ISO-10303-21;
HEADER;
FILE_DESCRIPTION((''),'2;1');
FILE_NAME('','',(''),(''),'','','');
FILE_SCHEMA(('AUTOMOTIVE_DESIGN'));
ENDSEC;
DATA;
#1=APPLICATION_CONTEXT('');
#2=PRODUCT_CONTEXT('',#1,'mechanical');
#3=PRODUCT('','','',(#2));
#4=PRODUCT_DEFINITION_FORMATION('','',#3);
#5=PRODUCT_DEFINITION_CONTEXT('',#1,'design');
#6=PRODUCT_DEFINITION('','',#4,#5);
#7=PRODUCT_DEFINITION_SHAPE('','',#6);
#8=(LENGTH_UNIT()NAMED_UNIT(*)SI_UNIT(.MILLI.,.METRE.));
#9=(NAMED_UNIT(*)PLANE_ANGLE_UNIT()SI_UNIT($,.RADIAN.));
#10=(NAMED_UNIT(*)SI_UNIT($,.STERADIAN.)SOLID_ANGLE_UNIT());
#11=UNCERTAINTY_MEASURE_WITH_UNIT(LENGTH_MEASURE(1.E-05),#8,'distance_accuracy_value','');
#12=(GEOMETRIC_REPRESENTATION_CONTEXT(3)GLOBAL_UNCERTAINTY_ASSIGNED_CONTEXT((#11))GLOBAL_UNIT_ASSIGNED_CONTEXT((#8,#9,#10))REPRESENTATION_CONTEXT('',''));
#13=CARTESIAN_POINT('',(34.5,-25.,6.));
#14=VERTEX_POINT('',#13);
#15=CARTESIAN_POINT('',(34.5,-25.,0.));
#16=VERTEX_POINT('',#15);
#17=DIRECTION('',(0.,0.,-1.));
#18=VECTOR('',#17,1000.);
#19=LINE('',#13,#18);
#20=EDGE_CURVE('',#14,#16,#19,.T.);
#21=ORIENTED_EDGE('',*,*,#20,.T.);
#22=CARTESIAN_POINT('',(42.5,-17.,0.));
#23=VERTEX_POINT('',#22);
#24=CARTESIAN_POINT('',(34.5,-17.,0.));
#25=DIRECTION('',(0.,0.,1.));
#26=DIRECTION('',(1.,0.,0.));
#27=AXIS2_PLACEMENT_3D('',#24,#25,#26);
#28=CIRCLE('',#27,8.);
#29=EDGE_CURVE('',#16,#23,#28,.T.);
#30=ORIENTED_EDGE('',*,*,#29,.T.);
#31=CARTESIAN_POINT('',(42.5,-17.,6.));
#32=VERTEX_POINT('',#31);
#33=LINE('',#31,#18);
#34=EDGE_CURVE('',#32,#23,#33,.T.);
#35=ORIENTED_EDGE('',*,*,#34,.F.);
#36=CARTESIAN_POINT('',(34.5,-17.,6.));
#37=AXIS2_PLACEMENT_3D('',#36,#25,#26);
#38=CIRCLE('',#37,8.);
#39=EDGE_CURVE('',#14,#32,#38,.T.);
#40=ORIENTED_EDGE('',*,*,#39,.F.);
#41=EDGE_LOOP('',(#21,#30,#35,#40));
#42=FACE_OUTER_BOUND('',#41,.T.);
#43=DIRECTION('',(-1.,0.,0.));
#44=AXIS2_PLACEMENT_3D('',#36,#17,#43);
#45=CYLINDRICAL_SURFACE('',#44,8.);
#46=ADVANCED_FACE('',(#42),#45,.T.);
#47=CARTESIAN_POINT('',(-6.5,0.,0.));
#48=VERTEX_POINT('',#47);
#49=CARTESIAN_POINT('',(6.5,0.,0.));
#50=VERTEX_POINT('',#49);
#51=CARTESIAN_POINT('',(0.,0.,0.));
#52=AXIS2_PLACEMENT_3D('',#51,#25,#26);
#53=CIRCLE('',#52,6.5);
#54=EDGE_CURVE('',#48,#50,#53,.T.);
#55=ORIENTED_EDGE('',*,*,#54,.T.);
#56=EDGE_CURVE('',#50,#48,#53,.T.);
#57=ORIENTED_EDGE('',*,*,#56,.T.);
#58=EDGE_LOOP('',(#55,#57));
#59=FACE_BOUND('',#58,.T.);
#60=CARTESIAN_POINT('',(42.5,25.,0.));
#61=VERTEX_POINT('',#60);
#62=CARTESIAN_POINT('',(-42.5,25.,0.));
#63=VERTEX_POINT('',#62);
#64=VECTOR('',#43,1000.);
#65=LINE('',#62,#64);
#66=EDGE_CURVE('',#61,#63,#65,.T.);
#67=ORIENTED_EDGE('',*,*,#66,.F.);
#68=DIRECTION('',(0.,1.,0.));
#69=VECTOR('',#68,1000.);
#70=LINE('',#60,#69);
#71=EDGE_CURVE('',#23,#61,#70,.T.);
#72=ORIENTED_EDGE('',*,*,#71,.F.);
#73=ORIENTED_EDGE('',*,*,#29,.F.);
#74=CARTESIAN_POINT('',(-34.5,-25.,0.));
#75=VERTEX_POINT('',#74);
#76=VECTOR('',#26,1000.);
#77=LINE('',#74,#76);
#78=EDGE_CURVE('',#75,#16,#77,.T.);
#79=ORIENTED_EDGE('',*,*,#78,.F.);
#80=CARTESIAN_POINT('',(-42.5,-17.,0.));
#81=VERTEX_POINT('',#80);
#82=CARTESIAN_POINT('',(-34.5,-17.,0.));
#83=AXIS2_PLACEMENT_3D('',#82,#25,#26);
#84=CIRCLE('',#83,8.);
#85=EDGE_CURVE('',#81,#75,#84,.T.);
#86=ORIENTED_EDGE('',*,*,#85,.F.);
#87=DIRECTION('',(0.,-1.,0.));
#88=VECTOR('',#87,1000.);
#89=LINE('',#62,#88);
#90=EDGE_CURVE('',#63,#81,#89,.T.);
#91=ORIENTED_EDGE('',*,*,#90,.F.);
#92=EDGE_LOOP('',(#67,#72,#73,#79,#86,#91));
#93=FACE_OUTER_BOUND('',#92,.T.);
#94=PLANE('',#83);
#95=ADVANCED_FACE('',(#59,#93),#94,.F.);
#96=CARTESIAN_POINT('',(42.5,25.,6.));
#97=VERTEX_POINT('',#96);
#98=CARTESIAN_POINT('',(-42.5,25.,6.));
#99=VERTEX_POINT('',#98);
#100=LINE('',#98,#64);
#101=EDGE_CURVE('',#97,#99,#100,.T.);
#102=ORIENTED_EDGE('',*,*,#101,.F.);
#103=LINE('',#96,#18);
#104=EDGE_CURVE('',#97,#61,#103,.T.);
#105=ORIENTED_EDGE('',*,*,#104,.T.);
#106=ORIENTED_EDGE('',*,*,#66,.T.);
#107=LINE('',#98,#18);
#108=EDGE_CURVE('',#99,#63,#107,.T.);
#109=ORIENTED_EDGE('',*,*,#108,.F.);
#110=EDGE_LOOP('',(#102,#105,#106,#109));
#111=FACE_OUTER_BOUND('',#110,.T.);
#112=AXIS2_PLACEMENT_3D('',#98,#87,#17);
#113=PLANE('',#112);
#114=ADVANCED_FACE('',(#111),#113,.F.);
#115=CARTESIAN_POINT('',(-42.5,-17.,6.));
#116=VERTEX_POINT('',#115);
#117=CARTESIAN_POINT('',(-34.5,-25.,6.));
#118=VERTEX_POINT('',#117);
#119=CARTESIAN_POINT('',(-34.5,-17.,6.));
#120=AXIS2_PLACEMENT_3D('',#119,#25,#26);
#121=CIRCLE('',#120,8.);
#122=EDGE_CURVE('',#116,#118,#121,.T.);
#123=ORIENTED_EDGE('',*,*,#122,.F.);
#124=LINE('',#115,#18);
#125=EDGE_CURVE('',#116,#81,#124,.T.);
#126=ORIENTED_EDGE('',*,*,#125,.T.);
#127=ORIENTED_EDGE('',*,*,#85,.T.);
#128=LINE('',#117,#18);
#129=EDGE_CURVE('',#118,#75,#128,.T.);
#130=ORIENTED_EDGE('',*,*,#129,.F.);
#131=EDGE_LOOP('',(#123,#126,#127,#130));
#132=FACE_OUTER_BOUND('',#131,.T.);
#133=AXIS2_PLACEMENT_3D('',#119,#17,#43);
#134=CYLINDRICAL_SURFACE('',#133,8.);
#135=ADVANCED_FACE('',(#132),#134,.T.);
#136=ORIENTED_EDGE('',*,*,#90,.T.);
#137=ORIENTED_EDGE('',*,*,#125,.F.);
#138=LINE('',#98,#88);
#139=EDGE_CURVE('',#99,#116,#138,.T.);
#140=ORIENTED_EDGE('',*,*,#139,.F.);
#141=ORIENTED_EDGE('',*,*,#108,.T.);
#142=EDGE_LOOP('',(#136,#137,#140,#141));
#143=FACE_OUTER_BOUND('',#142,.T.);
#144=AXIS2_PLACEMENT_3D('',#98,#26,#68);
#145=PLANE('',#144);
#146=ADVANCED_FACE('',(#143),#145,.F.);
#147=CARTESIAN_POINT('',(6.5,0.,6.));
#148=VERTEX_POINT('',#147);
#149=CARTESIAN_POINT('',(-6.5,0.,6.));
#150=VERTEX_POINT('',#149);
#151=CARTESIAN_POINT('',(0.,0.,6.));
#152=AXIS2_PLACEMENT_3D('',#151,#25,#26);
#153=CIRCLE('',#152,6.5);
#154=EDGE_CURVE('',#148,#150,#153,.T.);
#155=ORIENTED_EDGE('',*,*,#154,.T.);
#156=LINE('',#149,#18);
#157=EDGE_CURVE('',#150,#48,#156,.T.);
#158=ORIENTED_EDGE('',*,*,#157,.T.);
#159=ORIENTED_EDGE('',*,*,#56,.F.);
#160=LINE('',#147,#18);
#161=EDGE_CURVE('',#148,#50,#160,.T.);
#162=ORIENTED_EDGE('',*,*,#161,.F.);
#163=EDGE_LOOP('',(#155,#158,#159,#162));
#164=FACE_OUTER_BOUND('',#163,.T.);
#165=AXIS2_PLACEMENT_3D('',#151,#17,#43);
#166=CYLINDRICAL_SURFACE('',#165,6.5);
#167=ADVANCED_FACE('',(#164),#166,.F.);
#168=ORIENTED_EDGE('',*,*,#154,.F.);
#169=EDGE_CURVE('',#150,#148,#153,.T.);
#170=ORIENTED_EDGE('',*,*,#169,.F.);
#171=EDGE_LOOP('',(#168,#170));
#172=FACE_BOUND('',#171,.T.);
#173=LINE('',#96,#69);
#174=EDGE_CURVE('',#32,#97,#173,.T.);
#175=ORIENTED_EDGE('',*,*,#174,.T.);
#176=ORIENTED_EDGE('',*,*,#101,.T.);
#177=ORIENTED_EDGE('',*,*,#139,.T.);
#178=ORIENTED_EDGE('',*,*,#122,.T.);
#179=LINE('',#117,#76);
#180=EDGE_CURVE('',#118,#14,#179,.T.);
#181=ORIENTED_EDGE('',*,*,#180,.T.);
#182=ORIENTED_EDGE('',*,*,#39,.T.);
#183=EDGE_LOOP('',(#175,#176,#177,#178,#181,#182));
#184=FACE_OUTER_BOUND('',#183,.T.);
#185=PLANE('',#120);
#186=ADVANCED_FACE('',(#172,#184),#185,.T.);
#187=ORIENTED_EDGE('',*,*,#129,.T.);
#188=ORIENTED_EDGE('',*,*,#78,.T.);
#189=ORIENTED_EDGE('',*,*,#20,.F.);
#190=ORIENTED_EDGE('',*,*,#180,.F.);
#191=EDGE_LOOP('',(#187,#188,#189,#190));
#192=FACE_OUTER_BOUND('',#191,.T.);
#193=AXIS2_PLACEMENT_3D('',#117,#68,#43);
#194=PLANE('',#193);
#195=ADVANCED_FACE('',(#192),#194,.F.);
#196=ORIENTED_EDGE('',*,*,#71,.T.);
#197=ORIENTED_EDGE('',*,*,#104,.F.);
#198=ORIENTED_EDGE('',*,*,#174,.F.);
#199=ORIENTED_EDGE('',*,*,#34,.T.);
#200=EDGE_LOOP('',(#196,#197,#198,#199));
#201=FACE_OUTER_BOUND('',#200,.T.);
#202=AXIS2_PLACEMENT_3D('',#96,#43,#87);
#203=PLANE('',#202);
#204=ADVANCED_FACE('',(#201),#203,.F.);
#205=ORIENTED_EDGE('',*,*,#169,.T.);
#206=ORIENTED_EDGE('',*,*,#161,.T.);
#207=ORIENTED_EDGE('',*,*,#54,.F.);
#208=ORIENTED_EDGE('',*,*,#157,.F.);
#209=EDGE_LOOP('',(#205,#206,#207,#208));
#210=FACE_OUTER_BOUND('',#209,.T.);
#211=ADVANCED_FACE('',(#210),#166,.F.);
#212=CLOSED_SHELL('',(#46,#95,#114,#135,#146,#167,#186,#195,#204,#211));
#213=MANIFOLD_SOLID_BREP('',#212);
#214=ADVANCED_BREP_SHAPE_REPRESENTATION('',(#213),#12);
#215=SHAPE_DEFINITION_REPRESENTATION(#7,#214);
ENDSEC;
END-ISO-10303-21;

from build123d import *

# Parameters (mm, degrees)
SKETCH_1_R      = 6.5
EXTRUDE_1_DEPTH = 6


with BuildPart() as part:
    # 草图1 → 凸台-拉伸1 (new body)
    with BuildSketch(Plane.XY):
        with BuildLine():
            Line((-42.5, 25), (42.5, 25))
            Line((42.5, 25), (42.5, -17))
            ThreePointArc((42.5, -17), (40.156854249, -22.656854249), (34.5, -25))
            Line((34.5, -25), (-34.5, -25))
            ThreePointArc((-34.5, -25), (-40.156854249, -22.656854249), (-42.5, -17))
            Line((-42.5, -17), (-42.5, 25))
        make_face()
        Circle(SKETCH_1_R, mode=Mode.SUBTRACT)
    extrude(amount=EXTRUDE_1_DEPTH)


solid = part.part
